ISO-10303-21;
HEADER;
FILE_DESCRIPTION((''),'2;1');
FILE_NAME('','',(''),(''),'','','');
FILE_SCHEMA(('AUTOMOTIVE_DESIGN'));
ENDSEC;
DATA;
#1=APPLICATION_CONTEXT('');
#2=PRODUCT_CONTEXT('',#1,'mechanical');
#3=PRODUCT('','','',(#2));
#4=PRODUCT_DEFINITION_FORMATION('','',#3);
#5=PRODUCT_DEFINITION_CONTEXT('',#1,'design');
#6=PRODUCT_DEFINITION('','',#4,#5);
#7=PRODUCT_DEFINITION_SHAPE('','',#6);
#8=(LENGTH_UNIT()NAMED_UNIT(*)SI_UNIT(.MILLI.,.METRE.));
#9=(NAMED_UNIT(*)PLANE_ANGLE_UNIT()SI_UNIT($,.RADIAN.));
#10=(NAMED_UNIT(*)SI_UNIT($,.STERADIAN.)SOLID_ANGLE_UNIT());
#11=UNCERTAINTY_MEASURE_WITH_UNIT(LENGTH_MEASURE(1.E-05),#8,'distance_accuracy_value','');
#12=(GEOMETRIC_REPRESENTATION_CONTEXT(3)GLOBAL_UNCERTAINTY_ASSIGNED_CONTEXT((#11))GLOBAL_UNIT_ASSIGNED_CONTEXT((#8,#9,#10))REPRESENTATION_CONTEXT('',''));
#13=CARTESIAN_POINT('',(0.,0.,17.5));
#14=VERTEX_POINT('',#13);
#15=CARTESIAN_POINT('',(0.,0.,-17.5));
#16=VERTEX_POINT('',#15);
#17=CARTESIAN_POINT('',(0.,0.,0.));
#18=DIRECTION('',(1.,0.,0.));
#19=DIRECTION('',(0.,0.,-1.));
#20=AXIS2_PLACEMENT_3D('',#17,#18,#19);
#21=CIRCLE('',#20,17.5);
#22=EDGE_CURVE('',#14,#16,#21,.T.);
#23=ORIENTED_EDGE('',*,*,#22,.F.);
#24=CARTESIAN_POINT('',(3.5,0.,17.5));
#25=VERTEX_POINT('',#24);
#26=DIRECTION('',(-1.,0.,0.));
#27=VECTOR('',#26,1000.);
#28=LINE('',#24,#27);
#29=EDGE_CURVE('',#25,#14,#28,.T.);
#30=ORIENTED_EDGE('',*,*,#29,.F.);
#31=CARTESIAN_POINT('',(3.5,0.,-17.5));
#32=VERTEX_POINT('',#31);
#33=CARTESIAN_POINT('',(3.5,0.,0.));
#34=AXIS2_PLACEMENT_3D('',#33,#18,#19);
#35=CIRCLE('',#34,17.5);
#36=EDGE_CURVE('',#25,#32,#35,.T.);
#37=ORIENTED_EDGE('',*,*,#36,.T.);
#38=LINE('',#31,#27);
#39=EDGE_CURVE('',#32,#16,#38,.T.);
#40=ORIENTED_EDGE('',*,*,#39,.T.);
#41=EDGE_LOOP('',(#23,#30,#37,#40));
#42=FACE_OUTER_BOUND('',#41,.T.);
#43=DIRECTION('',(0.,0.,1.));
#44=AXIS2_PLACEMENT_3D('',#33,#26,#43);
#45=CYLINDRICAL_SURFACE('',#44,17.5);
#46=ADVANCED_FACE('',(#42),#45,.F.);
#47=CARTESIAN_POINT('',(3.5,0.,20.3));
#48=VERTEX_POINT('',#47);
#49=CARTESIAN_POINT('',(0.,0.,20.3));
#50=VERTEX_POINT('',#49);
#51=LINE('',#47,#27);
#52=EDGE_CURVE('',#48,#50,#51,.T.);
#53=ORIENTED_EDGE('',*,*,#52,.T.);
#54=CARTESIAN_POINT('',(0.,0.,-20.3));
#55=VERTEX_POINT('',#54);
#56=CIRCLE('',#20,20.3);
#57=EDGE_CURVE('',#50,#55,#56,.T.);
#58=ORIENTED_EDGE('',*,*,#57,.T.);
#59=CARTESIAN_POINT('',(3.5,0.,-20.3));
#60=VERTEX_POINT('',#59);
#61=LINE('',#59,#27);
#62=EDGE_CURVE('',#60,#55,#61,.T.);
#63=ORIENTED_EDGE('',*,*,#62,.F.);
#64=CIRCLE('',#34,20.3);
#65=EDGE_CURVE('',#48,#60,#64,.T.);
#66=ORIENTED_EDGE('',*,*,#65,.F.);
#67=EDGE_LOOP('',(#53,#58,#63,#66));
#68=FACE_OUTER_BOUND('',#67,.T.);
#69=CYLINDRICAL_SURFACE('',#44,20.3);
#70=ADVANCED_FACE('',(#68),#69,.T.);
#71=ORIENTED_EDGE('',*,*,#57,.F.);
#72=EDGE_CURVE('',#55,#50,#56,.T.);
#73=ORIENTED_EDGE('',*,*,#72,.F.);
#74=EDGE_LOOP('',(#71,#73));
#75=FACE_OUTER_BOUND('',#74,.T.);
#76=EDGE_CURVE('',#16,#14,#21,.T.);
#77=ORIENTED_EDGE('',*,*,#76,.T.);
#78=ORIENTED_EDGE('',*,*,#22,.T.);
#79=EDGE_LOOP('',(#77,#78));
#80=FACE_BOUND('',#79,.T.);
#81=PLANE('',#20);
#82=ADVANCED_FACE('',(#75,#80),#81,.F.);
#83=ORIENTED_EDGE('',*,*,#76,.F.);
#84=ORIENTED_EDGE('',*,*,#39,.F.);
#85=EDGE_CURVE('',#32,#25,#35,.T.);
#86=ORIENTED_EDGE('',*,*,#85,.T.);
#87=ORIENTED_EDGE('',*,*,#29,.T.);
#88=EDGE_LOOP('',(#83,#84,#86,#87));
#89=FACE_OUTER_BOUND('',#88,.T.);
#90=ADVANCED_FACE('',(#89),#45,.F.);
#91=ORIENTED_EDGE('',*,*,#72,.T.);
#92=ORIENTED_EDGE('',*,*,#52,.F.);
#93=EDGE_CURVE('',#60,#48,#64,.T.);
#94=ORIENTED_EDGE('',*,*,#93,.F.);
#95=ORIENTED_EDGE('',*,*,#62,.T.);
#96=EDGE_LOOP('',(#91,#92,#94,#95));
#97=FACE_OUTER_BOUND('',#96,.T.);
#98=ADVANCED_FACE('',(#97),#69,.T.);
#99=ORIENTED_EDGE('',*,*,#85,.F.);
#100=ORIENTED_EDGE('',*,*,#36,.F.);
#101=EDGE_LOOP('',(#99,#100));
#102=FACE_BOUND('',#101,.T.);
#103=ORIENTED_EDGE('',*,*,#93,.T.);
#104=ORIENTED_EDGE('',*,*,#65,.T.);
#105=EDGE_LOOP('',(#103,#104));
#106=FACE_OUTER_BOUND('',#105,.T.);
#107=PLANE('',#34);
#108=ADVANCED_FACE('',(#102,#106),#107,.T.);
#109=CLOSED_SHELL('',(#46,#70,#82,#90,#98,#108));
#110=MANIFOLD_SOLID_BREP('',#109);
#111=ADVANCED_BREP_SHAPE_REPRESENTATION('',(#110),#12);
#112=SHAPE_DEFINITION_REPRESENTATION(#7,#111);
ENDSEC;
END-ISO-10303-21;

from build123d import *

# Parameters (mm, degrees)
SKETCH1_R           = 20.3
SKETCH1_R_2         = 17.5
BOSS_EXTRUDE1_DEPTH = 3.5


with BuildPart() as part:
    # Sketch1 → Boss-Extrude1 (new body)
    with BuildSketch(Plane(origin=(0, 0, 0), x_dir=(0, 0, -1), z_dir=(1, 0, 0))):
        Circle(SKETCH1_R)
        Circle(SKETCH1_R_2, mode=Mode.SUBTRACT)
    extrude(amount=BOSS_EXTRUDE1_DEPTH)


solid = part.part
